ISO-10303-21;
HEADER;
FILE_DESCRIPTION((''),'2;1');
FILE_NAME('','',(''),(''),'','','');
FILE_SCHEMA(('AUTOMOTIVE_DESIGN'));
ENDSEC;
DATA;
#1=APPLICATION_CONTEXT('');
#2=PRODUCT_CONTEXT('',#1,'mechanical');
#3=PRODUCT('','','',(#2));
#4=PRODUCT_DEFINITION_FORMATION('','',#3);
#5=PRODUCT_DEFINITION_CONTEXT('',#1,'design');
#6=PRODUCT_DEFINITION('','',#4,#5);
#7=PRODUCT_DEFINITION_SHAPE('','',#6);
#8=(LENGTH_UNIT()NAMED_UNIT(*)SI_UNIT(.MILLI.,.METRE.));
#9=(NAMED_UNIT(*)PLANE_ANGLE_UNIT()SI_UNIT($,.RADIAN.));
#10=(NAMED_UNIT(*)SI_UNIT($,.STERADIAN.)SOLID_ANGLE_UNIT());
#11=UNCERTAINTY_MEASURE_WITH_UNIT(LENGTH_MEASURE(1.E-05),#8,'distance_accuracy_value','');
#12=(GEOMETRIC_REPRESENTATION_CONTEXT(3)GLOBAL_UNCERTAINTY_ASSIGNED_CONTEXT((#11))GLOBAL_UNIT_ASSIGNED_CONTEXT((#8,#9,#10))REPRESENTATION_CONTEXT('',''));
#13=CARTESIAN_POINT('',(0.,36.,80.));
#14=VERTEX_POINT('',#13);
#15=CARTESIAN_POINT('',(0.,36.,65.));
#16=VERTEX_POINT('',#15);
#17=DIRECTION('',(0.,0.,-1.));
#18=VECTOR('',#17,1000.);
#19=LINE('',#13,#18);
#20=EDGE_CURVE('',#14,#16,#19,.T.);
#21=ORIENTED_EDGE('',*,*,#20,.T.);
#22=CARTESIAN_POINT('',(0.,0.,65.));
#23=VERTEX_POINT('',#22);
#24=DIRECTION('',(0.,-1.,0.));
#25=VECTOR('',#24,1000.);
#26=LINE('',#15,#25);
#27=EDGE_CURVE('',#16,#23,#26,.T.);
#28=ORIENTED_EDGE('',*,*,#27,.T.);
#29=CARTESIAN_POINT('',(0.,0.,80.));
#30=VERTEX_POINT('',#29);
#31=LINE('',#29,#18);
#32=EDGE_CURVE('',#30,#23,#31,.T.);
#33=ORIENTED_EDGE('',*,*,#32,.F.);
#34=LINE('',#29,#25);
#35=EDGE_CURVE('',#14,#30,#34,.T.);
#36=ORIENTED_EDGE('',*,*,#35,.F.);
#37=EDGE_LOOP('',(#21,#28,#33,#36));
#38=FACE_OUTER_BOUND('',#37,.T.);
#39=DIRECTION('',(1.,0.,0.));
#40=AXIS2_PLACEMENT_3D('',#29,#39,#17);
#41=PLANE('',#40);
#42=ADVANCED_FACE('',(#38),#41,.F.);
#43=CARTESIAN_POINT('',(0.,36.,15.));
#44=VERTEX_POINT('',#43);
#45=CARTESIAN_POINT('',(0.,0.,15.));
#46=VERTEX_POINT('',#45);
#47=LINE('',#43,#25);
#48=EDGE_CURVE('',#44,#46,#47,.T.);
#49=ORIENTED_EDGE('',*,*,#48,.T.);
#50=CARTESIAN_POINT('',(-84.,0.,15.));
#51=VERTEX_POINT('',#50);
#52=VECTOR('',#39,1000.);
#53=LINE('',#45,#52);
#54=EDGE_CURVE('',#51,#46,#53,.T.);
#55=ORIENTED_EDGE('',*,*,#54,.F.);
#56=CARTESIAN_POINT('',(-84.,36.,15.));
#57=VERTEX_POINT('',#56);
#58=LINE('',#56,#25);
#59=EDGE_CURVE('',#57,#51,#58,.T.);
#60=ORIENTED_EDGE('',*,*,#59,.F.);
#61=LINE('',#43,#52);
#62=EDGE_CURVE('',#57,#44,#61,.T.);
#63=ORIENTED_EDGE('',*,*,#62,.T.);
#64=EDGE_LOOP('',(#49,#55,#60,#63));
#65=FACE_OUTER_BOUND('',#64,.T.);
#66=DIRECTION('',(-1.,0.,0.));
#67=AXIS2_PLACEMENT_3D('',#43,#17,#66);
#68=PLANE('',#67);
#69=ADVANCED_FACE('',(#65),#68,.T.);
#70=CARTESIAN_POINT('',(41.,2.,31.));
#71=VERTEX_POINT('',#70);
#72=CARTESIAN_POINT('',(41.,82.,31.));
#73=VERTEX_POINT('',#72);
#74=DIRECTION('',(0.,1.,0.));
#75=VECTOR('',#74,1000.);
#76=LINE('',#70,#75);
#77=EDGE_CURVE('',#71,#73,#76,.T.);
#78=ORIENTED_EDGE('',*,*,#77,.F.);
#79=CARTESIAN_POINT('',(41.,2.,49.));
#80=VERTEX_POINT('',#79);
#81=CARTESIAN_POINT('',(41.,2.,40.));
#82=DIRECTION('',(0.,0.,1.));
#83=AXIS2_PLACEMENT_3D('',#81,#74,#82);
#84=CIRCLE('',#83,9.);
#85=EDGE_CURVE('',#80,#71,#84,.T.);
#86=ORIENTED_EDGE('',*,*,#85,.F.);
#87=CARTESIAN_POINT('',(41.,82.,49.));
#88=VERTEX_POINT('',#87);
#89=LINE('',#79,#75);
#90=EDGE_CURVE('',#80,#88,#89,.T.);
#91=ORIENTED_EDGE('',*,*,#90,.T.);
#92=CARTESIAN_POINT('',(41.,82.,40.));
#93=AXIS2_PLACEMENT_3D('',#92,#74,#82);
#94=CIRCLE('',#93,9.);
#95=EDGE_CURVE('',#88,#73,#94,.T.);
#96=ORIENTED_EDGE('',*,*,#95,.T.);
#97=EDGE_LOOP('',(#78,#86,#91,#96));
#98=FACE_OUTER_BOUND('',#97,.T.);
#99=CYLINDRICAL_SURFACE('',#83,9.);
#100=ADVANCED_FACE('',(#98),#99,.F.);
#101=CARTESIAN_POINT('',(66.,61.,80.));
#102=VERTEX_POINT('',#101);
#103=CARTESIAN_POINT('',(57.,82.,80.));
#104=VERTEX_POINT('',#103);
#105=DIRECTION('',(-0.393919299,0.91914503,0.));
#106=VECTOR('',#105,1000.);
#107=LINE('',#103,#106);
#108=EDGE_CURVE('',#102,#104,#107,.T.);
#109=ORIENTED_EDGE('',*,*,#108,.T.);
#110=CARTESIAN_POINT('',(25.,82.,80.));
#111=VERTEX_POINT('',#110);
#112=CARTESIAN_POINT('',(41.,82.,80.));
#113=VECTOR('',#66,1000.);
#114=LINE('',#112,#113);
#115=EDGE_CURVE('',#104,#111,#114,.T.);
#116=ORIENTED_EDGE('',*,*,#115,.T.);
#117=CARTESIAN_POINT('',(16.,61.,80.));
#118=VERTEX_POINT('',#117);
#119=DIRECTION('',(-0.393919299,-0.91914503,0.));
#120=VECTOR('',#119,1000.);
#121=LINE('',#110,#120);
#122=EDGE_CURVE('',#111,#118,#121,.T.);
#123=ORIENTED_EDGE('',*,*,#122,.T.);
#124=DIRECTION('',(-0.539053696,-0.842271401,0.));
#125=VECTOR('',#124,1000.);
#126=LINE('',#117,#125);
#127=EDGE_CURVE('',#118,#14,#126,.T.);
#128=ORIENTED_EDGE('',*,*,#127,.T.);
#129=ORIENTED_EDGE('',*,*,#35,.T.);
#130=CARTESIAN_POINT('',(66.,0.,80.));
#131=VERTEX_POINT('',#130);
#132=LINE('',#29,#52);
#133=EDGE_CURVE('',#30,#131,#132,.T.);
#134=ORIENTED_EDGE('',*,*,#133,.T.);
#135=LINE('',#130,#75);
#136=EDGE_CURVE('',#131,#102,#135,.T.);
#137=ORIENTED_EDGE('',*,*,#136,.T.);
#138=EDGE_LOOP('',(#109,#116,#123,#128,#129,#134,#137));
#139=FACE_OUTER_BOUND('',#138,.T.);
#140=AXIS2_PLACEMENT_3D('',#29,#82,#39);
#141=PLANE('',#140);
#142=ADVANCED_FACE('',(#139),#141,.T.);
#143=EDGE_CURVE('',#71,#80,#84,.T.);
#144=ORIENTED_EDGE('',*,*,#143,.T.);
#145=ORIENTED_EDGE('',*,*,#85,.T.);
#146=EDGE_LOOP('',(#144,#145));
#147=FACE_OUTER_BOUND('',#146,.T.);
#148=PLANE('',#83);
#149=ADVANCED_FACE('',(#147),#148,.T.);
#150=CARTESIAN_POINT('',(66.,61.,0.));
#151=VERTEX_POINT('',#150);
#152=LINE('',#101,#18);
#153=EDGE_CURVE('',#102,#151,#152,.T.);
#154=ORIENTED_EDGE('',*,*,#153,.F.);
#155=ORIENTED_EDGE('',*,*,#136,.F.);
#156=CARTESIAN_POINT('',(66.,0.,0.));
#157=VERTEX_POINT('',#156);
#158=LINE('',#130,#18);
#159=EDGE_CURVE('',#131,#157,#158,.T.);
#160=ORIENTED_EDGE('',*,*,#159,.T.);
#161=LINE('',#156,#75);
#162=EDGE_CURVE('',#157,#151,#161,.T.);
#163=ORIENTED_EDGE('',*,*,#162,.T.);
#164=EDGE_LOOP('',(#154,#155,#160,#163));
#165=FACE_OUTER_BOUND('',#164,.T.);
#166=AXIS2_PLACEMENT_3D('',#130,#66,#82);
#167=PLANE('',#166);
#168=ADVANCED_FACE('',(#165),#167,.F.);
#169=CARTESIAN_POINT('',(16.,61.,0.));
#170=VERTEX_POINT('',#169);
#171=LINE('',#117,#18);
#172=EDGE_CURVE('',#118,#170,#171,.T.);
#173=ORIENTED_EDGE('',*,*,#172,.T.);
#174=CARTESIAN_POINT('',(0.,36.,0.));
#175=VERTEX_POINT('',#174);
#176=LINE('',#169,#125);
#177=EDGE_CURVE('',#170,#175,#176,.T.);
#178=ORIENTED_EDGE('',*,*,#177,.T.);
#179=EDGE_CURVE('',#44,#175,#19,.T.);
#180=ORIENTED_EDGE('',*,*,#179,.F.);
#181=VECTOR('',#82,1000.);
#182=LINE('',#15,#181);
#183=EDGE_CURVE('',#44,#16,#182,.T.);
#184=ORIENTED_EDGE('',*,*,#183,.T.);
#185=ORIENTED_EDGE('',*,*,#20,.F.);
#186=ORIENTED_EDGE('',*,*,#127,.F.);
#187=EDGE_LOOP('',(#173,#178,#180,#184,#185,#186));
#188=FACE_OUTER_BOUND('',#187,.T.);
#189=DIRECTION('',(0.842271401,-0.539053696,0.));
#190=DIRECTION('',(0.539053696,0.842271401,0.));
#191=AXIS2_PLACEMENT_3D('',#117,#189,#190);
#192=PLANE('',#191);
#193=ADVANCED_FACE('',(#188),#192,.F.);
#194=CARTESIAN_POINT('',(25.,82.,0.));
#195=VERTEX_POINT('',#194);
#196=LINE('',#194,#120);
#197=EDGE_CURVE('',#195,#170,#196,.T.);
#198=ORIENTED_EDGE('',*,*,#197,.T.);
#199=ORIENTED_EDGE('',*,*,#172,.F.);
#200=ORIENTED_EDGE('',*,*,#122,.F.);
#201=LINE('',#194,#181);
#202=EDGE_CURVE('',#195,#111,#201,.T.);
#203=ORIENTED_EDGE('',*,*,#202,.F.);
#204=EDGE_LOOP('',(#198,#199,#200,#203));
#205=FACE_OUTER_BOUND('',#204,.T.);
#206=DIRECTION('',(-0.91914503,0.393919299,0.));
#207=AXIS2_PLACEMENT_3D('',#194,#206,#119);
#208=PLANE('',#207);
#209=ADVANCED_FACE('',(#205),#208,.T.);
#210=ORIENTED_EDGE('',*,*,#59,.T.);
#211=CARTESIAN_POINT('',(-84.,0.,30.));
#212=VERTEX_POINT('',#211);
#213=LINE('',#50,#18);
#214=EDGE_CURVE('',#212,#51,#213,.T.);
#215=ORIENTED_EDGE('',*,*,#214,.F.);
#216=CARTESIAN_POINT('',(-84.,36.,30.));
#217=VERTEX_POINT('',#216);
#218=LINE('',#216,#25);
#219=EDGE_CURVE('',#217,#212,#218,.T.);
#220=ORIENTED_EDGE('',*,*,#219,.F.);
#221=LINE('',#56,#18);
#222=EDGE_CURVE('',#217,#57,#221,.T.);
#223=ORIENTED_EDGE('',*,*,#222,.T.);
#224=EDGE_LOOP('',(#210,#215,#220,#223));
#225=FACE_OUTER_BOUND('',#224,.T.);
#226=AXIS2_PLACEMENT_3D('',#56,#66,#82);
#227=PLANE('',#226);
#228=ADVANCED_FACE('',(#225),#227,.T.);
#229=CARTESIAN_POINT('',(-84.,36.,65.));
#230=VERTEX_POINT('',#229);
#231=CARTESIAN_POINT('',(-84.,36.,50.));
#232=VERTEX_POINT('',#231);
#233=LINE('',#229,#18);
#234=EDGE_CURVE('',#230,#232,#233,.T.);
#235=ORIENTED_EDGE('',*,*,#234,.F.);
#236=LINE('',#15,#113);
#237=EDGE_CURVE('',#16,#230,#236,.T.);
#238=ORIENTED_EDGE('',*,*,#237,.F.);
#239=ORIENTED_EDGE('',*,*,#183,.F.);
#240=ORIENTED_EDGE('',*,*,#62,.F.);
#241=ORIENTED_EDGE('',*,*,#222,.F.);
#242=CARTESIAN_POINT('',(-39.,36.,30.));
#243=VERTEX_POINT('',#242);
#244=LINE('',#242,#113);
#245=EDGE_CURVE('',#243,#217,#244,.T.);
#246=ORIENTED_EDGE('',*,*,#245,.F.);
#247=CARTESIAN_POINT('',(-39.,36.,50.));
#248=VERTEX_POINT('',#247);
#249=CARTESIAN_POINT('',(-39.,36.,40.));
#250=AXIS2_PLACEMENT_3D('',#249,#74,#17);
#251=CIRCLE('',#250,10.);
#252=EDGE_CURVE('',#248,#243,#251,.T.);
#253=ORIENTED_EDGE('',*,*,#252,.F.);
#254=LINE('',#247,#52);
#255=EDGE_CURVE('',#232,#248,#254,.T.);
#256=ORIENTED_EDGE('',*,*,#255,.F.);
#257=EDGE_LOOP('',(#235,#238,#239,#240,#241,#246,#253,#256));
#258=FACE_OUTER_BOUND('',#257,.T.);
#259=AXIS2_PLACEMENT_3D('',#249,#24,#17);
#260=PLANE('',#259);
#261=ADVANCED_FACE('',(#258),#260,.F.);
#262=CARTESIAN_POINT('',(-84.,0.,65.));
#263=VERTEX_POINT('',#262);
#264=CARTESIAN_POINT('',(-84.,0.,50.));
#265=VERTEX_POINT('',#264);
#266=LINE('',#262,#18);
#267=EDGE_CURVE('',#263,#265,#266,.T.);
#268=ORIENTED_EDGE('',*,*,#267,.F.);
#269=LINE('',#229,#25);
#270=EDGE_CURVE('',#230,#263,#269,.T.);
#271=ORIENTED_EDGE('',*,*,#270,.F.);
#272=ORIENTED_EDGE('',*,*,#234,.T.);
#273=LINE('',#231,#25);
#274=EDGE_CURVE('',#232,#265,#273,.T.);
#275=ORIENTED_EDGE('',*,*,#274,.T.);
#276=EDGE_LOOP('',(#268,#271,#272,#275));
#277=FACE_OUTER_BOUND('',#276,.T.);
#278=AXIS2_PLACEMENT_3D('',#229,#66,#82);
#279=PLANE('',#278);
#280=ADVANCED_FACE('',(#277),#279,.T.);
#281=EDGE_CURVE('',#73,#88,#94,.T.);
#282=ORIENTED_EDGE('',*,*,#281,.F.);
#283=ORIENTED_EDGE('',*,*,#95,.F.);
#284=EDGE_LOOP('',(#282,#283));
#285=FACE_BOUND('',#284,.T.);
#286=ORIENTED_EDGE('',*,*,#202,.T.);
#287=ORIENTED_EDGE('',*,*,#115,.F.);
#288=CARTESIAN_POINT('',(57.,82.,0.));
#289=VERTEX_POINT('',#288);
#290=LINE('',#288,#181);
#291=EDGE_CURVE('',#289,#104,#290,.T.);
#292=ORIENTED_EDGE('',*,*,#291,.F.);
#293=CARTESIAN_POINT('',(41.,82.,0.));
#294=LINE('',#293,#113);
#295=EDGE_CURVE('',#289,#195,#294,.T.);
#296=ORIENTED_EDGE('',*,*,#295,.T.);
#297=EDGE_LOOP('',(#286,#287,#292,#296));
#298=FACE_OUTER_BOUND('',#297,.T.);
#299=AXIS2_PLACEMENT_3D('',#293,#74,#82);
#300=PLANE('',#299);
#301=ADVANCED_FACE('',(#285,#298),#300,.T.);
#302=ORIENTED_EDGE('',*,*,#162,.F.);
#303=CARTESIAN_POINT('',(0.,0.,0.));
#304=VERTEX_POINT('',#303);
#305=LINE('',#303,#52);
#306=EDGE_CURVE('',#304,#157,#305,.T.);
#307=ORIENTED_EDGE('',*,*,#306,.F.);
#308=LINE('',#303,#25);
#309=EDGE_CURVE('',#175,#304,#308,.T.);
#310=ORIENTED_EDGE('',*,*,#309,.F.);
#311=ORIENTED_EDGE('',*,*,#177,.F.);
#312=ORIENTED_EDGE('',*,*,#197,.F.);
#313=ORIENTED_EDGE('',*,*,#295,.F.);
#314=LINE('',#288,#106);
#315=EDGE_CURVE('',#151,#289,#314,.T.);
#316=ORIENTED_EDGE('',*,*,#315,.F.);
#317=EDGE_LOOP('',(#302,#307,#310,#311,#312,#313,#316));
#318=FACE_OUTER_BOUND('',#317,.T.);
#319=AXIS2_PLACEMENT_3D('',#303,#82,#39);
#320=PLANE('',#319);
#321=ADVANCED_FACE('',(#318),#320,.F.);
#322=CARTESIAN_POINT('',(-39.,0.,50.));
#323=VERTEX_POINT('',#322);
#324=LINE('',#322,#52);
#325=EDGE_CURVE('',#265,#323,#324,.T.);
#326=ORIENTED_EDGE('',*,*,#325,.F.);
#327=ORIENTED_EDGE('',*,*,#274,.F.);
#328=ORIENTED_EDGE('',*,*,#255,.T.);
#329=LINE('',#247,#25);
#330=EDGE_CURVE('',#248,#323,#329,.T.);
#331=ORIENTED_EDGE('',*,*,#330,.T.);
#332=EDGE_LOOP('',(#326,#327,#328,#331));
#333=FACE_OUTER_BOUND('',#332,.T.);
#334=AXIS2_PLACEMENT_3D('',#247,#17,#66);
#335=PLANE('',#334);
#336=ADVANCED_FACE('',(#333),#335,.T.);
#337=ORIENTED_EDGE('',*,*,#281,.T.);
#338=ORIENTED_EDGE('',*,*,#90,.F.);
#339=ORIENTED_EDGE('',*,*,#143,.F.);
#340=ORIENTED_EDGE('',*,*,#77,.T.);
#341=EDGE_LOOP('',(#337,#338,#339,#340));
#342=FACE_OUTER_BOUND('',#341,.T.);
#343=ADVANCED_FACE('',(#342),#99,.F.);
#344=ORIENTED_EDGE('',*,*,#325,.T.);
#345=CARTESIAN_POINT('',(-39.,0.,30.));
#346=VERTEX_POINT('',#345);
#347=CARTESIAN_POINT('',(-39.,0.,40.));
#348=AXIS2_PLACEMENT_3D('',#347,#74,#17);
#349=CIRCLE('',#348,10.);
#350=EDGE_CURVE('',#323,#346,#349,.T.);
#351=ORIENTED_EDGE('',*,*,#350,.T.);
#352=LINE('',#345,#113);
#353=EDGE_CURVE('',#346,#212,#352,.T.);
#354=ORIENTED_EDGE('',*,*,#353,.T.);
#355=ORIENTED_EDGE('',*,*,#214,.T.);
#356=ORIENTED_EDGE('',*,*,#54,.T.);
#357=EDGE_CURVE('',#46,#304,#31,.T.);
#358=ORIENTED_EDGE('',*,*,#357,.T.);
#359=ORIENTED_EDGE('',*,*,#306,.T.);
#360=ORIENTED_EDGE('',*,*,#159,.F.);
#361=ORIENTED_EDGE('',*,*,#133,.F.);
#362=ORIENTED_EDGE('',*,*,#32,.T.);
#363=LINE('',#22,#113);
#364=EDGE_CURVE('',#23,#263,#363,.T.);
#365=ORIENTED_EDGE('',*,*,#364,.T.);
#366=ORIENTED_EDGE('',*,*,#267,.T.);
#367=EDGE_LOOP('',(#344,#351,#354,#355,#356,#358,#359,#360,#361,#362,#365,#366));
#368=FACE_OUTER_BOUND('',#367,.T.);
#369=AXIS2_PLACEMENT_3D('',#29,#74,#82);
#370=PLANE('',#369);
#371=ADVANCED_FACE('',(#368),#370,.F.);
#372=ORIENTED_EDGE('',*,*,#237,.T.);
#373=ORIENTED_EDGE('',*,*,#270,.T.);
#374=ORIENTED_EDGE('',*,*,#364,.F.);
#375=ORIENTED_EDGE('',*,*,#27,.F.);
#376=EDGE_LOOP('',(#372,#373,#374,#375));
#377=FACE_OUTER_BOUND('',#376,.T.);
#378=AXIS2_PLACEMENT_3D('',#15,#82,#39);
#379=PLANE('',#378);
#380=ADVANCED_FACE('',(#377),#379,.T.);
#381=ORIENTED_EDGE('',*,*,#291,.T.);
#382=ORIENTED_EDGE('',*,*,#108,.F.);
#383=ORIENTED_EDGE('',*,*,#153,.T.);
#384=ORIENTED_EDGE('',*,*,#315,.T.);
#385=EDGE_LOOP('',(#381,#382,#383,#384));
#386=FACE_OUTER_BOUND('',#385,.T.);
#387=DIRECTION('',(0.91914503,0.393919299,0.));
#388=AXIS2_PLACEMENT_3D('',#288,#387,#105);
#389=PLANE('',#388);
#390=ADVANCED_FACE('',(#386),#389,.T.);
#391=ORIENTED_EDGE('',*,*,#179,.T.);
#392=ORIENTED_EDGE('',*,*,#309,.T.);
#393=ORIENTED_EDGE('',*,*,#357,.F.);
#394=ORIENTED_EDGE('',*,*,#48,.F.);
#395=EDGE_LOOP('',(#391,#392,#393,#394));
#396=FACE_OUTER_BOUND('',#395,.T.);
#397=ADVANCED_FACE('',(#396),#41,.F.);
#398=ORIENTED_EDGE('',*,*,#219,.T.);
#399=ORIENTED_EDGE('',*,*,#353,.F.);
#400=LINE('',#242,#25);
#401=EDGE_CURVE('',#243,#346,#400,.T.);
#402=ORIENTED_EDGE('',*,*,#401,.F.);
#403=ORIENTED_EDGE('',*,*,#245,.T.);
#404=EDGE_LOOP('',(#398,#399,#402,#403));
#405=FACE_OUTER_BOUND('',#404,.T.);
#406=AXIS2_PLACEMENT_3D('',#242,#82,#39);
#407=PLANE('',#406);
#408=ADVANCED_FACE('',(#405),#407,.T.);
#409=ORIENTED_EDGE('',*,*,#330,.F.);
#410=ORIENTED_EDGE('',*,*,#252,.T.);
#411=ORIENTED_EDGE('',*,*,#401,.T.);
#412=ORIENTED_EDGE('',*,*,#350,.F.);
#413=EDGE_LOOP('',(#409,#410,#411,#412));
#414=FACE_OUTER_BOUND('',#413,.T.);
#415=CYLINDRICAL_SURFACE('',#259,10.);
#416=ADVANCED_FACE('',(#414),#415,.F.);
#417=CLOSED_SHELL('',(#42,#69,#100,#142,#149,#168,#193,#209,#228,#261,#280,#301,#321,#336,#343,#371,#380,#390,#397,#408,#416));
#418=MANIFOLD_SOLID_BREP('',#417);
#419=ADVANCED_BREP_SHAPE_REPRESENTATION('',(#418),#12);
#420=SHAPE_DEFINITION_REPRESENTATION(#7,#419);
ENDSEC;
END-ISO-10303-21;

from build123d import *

# Parameters (mm, degrees)
MAIN_BLOCK_DEPTH      = 80
BLOCK_EXTENSION_DEPTH = 80
HOLE_18_SKETCH_R      = 9
THROUGH_HOLE_18_DEPTH = 80
SLOTTED_ARM_DEPTH     = 36


with BuildPart() as part:
    # Main Block Profile → Main Block (new body)
    with BuildSketch(Plane.XY):
        Polygon((0, 0), (66, 0), (66, 61), (16, 61), (0, 36), align=None)
    extrude(amount=MAIN_BLOCK_DEPTH)

    # Block Extension Profile → Block Extension (add)
    with BuildSketch(Plane.XY.offset(80)):
        Polygon((41, 82), (57, 82), (66, 61), (16, 61), (25, 82), align=None)
    extrude(amount=-BLOCK_EXTENSION_DEPTH)

    # Hole Ø18 Sketch → Through Hole Ø18 (cut)
    with BuildSketch(Plane(origin=(0, 82, 0), x_dir=(1, 0, 0), z_dir=(0, 1, 0))):
        with Locations(Location((41, -40, 0), (0, 0, 270))):
            Circle(HOLE_18_SKETCH_R)
    extrude(amount=-THROUGH_HOLE_18_DEPTH, mode=Mode.SUBTRACT)

    # Slotted Arm Profile → Slotted Arm (add)
    with BuildSketch(Plane.XZ):
        with BuildLine():
            Line((0, 65), (0, 15))
            Line((0, 15), (-84, 15))
            Line((-84, 15), (-84, 30))
            Line((-84, 30), (-39, 30))
            ThreePointArc((-39, 30), (-29, 40), (-39, 50))
            Line((-39, 50), (-84, 50))
            Line((-84, 50), (-84, 65))
            Line((-84, 65), (0, 65))
        make_face()
    extrude(amount=-SLOTTED_ARM_DEPTH)


solid = part.part
